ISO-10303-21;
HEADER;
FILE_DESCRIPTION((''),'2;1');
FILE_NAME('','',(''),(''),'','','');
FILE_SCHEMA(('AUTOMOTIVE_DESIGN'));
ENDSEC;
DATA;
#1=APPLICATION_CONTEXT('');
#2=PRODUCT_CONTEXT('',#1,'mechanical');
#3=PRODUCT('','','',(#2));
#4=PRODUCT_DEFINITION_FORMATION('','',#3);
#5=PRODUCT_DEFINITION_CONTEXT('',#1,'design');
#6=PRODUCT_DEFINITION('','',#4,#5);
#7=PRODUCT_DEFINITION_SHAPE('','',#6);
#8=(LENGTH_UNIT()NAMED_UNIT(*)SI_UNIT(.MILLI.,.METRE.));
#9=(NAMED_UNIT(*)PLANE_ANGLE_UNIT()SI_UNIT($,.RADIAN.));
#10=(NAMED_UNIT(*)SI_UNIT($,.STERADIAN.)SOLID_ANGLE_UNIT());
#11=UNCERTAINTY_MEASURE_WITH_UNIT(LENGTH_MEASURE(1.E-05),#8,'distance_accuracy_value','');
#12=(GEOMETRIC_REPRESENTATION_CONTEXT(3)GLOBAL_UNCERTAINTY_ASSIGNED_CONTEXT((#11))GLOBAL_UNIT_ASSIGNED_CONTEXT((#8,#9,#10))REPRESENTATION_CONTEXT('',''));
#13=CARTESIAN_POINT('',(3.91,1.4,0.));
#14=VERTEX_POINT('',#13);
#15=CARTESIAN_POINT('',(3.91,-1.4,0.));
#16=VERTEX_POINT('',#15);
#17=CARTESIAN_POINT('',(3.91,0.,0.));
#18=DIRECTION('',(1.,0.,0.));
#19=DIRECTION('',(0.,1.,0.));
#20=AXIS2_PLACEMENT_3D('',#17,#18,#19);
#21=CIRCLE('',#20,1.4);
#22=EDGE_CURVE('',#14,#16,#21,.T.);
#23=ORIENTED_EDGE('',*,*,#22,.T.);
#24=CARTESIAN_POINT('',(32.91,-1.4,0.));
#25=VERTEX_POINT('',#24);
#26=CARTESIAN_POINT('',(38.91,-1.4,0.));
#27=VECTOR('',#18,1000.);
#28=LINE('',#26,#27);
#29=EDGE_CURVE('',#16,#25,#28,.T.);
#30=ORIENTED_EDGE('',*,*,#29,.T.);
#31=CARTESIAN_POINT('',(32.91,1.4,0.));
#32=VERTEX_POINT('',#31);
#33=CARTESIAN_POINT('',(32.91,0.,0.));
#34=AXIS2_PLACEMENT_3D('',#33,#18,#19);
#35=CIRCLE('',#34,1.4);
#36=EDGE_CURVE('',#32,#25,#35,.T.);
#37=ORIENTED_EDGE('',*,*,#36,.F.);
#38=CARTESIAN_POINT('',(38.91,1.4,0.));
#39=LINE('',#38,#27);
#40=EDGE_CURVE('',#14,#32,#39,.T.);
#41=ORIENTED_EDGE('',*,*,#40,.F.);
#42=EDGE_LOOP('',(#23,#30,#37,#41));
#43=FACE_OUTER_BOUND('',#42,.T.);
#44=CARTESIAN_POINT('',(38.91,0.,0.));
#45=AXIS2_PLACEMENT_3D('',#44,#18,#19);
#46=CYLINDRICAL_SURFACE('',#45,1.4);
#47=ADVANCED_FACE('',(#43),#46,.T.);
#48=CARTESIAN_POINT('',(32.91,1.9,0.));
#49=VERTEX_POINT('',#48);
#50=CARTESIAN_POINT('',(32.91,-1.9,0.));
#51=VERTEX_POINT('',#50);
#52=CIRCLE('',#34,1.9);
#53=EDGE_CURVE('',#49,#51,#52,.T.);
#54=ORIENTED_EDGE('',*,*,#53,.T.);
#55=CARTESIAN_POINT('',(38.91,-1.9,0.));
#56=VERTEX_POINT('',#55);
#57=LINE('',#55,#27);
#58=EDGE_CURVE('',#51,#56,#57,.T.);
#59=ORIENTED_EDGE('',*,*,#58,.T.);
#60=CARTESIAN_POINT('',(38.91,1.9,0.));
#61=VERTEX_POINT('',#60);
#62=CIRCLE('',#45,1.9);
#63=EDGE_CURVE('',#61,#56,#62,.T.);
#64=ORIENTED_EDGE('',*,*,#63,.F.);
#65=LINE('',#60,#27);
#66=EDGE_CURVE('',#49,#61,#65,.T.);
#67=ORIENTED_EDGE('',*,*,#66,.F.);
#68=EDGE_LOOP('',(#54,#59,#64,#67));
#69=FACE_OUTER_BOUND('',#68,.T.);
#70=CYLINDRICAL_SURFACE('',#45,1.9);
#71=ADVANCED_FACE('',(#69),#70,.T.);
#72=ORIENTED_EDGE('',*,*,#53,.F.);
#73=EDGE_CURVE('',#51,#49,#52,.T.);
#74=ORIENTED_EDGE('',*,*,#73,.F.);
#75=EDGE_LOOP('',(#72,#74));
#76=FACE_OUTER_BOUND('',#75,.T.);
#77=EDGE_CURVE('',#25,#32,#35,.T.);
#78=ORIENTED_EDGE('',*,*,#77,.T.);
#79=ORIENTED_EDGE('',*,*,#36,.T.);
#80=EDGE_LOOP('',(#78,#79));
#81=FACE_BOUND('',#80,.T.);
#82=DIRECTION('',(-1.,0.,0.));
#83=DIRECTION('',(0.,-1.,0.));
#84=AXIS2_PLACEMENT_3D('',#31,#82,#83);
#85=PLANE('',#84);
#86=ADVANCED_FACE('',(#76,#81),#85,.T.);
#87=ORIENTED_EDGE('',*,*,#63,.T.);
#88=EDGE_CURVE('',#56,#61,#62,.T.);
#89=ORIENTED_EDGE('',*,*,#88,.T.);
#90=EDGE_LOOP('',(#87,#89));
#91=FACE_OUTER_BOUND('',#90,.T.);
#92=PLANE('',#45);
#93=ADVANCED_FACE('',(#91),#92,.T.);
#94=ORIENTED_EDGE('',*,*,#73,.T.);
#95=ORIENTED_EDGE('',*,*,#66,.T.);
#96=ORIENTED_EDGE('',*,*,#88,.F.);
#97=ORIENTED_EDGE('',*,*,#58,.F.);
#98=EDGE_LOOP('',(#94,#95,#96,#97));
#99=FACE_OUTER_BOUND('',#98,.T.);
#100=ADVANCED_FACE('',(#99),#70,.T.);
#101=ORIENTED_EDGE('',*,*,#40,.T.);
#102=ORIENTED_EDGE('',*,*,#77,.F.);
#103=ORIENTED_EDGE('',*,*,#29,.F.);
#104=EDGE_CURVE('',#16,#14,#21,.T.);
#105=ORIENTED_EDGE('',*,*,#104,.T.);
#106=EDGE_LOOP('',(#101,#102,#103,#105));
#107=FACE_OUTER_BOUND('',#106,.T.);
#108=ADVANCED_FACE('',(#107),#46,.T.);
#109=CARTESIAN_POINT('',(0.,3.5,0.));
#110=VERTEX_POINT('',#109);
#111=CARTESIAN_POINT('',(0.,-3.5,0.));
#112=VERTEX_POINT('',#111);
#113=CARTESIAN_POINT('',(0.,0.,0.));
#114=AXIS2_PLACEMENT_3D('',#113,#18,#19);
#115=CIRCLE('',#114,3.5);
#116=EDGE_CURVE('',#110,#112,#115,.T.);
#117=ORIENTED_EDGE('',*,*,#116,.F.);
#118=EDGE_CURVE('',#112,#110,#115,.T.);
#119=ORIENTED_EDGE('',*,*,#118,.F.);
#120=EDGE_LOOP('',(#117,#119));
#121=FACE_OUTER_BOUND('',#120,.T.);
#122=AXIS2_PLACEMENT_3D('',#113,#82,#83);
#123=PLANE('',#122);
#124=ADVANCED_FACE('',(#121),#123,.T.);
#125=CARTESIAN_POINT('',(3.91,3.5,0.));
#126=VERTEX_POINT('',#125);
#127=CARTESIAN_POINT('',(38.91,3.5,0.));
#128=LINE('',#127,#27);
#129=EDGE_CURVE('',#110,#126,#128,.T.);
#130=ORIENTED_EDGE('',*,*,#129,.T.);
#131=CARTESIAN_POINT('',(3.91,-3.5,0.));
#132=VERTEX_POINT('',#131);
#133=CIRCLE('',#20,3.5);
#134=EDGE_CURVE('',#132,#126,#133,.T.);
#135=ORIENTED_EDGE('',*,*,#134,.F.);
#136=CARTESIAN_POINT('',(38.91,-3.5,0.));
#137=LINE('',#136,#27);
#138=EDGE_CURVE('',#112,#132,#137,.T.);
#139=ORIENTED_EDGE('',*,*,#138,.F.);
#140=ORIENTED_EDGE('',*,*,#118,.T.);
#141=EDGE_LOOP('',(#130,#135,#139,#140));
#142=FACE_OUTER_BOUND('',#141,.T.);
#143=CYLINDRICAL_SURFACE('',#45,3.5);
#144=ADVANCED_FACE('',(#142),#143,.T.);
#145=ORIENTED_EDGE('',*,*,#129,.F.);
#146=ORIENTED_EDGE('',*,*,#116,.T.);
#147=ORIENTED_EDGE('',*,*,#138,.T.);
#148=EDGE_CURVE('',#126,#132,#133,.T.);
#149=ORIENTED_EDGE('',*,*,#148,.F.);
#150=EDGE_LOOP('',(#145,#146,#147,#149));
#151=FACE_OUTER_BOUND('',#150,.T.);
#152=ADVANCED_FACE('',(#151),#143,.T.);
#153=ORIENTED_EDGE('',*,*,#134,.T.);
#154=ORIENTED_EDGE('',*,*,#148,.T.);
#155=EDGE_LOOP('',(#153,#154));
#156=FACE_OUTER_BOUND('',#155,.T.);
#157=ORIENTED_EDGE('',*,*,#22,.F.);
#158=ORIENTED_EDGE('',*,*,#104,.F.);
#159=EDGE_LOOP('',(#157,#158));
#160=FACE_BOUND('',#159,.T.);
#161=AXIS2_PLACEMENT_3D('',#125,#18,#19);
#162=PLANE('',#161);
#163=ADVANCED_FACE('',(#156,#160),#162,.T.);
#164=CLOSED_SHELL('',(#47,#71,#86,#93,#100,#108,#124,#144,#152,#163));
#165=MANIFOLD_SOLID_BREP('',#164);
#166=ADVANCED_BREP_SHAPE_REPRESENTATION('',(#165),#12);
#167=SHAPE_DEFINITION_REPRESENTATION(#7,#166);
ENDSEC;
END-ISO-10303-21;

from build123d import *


with BuildPart() as part:
    # Sketch1 → Revolve1 (revolve)
    with BuildSketch(Plane.XY):
        Polygon((0, 0), (0, 3.5), (3.91, 3.5), (3.91, 1.4), (32.91, 1.4), (32.91, 1.9), (38.91, 1.9), (38.91, 0), align=None)
    revolve(axis=Axis((38.91, 0, 0), (-1, 0, 0)))


solid = part.part
